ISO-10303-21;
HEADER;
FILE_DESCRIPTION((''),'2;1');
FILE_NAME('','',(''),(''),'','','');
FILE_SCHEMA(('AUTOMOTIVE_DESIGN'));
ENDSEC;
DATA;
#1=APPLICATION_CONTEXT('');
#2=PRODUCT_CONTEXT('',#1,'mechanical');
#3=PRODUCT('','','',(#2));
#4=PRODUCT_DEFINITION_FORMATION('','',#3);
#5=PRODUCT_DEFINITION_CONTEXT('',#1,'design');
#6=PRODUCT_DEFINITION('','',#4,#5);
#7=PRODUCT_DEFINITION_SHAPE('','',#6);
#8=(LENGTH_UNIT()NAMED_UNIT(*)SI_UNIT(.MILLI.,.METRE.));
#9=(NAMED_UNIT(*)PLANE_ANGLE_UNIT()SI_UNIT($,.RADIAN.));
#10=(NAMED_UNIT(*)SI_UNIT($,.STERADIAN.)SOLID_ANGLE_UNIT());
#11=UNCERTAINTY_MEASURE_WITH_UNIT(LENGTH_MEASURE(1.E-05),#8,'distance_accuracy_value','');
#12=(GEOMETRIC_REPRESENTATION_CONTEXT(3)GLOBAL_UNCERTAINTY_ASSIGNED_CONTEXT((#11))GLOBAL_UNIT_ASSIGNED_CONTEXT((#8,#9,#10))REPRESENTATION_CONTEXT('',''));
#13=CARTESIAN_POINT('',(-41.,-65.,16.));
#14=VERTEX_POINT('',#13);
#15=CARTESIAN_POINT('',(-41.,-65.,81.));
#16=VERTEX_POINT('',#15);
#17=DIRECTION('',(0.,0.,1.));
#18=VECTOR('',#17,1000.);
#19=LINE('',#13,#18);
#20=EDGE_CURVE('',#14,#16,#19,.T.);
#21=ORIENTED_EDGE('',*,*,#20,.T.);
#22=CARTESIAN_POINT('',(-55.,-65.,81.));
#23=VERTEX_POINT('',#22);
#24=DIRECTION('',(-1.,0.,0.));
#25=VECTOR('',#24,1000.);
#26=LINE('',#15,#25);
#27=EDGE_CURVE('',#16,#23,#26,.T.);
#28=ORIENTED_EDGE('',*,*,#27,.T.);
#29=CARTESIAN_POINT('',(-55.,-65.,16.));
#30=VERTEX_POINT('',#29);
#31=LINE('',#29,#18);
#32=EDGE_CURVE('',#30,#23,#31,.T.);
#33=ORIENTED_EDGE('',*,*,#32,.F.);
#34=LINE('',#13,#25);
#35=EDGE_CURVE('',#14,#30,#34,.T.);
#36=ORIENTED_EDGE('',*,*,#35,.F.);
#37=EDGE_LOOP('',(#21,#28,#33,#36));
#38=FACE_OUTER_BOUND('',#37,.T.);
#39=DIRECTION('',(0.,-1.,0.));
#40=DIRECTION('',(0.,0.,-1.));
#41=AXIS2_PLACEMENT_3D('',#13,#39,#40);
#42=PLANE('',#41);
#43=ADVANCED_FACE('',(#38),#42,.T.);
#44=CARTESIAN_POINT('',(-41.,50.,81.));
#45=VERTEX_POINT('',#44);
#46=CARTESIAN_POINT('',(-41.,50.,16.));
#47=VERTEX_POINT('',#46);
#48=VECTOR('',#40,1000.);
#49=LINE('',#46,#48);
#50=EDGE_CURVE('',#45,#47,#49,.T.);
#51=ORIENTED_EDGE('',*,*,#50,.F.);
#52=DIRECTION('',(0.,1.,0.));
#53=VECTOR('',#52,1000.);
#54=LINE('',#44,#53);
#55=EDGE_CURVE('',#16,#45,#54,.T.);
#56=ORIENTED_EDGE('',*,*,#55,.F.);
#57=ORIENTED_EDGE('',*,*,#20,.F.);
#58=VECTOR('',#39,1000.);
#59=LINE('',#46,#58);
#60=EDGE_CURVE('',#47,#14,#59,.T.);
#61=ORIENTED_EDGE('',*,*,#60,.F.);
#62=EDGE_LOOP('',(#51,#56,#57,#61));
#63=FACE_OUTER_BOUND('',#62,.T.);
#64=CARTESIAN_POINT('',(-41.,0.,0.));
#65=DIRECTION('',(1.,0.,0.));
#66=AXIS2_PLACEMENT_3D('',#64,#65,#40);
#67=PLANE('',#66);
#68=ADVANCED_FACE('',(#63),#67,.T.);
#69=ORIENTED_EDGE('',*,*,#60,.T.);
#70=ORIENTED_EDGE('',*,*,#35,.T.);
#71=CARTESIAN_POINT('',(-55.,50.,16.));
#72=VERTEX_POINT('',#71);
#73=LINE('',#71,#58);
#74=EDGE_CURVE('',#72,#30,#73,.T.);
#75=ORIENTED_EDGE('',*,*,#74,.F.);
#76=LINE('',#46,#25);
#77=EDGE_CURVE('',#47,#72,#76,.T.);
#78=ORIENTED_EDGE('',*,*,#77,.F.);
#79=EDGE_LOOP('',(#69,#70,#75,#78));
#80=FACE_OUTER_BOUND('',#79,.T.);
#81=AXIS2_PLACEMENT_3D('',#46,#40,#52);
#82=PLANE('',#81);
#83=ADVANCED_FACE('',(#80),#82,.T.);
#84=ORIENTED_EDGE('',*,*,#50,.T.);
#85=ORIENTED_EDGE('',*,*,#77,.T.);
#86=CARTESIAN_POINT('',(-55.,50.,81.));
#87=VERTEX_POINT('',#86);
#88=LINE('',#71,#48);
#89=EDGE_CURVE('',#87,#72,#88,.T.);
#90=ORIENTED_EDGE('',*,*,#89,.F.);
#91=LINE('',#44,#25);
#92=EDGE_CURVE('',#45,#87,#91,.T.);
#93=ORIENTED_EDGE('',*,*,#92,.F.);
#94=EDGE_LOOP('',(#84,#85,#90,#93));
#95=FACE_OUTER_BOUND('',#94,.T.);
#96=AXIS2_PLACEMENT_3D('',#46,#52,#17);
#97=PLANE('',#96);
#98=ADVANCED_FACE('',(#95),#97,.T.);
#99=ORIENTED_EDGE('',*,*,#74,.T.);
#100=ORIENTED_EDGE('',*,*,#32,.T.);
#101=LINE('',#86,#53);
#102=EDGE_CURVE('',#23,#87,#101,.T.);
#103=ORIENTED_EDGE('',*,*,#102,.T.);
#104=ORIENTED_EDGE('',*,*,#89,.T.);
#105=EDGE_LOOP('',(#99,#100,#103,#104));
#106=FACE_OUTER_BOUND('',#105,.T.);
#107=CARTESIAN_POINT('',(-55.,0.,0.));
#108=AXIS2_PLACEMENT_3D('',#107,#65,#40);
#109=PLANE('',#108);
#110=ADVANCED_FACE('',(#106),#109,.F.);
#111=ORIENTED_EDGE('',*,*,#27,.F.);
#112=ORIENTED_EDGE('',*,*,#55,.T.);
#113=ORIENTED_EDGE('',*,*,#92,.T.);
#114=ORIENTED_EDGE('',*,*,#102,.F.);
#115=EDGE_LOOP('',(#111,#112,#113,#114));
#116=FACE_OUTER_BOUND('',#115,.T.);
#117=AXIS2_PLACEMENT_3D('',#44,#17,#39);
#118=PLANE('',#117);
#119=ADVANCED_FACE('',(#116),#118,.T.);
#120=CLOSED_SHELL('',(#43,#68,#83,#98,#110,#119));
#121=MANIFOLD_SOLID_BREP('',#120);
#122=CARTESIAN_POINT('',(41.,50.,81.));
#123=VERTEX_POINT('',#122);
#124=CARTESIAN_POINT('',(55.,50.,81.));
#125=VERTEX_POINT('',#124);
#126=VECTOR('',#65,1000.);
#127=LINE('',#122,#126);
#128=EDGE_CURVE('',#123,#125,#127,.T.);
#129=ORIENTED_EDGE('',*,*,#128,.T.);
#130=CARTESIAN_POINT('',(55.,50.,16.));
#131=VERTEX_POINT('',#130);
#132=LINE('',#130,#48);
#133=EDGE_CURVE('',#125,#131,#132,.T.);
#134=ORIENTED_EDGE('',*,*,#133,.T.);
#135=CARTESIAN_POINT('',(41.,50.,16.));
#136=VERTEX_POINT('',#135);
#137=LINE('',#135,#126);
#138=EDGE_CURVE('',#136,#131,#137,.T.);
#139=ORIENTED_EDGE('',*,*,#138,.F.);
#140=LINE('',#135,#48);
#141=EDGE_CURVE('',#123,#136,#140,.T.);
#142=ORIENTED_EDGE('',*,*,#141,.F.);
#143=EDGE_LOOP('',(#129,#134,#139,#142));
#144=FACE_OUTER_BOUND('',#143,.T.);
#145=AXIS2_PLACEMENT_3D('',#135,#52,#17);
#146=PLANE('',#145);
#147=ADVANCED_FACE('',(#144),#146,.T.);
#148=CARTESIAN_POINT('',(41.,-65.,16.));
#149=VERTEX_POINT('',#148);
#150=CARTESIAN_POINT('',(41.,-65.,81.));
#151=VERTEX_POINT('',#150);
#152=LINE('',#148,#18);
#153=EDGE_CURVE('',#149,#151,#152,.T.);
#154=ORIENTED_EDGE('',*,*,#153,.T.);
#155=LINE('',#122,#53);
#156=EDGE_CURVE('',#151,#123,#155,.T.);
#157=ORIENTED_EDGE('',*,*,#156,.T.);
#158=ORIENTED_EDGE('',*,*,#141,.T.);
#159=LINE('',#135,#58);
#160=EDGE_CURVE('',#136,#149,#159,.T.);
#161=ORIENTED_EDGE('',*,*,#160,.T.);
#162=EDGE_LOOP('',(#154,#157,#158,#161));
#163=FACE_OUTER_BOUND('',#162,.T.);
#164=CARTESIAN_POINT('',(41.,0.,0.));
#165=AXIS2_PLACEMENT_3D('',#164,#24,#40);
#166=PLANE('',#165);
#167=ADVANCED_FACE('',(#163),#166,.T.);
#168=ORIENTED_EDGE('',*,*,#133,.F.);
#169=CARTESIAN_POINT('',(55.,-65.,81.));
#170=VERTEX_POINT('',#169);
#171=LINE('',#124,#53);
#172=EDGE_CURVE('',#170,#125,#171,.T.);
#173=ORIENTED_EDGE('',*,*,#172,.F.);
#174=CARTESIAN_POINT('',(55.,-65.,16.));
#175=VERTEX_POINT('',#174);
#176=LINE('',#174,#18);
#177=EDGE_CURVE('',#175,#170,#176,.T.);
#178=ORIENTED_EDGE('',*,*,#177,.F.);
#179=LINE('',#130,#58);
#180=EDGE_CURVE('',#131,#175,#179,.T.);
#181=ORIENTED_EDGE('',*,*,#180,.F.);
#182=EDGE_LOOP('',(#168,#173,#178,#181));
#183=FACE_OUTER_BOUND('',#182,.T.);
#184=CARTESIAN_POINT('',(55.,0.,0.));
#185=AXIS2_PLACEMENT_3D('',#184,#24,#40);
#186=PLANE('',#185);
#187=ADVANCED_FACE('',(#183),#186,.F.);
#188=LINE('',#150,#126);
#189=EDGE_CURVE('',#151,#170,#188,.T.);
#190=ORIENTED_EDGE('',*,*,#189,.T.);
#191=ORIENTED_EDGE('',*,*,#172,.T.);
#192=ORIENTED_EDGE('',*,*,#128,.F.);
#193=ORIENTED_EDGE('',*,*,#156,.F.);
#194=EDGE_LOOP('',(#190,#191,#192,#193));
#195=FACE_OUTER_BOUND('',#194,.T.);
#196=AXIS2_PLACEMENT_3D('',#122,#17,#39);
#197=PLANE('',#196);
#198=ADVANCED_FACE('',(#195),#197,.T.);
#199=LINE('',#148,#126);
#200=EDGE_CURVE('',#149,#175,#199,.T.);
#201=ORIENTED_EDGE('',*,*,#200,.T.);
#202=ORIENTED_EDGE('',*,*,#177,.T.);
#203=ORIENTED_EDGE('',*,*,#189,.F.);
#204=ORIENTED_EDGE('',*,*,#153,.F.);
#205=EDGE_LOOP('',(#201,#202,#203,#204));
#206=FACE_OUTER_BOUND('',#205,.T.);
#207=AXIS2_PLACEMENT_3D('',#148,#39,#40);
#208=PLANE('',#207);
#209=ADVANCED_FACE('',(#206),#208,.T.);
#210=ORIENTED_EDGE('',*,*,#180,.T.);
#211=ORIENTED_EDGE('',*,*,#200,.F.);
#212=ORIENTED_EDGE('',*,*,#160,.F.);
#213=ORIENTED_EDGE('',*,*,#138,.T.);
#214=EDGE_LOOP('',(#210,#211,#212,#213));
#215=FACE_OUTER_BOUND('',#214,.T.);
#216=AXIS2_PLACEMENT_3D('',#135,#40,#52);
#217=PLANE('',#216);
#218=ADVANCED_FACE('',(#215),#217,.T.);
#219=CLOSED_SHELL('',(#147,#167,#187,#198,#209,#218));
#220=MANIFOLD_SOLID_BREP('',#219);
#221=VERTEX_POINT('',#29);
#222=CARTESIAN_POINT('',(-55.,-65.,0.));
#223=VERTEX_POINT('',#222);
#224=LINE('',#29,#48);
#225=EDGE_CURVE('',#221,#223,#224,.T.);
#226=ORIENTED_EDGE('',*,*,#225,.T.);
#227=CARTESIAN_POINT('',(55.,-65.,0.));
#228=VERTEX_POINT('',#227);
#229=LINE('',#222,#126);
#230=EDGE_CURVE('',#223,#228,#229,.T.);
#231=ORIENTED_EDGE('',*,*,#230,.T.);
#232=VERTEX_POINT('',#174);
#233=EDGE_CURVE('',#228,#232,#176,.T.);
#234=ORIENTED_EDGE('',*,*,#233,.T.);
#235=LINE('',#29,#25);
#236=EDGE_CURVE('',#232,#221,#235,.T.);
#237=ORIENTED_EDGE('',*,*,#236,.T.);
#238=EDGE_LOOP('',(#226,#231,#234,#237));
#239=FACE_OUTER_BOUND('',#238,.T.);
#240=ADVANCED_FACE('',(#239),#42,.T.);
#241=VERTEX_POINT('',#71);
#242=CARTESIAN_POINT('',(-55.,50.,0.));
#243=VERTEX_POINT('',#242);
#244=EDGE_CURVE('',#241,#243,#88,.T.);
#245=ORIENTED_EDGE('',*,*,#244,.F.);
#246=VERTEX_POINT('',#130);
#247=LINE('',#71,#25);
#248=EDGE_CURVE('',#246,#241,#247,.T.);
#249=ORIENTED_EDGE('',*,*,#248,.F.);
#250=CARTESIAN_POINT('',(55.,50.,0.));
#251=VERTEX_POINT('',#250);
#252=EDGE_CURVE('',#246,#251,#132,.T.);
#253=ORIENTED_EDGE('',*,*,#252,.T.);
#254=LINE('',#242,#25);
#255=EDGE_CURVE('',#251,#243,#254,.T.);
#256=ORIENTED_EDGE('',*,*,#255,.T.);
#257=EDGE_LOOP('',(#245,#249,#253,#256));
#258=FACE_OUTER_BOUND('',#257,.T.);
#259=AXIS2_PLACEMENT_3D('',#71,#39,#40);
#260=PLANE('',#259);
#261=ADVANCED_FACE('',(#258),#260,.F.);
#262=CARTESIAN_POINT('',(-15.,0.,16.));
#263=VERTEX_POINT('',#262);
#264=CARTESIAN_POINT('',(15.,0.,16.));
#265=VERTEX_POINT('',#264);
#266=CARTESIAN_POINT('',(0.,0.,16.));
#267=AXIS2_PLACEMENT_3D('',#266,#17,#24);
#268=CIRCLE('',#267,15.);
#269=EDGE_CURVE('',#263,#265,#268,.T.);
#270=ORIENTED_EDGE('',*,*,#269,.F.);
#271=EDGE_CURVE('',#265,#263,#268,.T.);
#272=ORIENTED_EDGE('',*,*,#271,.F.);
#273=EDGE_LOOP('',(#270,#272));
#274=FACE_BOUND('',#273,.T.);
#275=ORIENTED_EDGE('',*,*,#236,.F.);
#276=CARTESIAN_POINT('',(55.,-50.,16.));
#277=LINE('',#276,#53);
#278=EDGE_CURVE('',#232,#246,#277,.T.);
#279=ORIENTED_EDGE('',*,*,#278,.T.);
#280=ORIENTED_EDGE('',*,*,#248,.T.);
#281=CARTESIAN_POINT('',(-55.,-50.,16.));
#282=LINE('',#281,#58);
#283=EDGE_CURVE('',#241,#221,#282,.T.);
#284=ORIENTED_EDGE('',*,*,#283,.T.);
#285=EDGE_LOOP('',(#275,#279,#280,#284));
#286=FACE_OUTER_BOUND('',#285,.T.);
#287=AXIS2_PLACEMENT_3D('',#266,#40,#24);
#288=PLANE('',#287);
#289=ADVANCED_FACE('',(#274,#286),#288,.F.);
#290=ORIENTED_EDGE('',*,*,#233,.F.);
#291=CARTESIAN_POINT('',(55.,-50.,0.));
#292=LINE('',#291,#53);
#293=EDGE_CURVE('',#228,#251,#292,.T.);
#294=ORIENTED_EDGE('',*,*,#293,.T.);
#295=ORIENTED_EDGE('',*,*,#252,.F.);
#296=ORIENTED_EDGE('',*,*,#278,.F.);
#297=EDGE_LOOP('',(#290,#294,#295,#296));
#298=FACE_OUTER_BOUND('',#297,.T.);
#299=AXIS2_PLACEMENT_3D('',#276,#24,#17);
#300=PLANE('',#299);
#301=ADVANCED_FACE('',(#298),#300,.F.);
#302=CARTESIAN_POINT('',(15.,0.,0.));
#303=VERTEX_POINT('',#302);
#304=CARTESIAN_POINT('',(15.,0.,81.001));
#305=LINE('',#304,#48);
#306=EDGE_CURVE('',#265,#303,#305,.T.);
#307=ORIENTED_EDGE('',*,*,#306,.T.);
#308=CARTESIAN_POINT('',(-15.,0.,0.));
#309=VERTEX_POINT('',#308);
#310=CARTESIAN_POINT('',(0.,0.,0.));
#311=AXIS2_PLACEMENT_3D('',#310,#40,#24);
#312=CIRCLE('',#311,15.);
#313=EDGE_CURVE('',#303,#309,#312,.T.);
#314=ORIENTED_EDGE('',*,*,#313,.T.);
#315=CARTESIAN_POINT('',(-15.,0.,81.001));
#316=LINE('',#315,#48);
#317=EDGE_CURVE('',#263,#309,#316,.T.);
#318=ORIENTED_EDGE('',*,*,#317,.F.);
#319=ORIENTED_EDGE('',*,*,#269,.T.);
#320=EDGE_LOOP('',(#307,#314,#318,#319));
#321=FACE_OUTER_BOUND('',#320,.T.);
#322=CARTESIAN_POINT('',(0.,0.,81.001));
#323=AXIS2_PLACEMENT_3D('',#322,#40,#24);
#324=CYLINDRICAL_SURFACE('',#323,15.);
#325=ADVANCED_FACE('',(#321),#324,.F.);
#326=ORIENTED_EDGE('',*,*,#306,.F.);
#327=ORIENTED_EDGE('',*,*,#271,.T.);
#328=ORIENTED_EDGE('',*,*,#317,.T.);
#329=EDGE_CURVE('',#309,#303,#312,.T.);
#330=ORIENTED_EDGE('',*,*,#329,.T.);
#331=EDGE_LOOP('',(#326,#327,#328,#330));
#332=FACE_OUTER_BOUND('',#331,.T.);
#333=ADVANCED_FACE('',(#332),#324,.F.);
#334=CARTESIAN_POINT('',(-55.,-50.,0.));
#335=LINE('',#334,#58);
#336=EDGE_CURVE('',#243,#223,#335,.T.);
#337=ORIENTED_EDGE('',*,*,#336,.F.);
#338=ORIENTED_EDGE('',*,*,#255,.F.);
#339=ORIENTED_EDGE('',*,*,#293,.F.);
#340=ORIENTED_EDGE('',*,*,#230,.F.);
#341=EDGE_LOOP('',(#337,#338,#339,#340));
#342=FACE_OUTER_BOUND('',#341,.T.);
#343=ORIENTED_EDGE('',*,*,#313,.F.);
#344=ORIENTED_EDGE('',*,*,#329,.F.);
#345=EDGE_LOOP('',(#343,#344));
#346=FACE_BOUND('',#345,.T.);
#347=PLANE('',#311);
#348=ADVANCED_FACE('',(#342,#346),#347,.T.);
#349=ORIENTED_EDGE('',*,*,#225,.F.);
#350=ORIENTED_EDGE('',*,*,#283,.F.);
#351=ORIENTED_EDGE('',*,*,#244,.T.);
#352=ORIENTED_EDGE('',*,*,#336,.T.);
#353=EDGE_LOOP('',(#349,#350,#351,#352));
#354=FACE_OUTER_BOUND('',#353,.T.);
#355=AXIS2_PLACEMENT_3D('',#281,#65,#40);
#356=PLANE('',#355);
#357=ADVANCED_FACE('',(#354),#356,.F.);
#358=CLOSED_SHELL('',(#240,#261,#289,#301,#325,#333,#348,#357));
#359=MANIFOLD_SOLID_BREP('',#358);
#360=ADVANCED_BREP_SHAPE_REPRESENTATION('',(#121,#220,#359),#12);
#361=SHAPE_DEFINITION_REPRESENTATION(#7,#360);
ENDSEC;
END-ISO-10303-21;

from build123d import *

# Parameters (mm, degrees)
SKETCH_1_W          = 110
SKETCH_1_H          = 100
EXTRUDE_1_DEPTH     = 16
SKETCH_2_W          = 65
SKETCH_2_H          = 115
EXTRUDE_2_DEPTH     = 14
SKETCH_3_R          = 15
CUT_EXTRUDE_1_DEPTH = 16
SKETCH_4_W          = 110
SKETCH_4_H          = 16
EXTRUDE_3_DEPTH     = 15


with BuildPart() as part:
    # 草图1 → 凸台-拉伸1 (new body)
    with BuildSketch(Plane.XY):
        Rectangle(SKETCH_1_W, SKETCH_1_H)
    extrude(amount=EXTRUDE_1_DEPTH)

    # 草图3 → 切除-拉伸1 (cut)
    with BuildSketch(Plane(origin=(0, 0, 0), x_dir=(-1, 0, 0), z_dir=(0, 0, -1))):
        Circle(SKETCH_3_R)
    extrude(amount=-CUT_EXTRUDE_1_DEPTH, mode=Mode.SUBTRACT)

    # 草图4 → 凸台-拉伸3 (add)
    with BuildSketch(Plane.XZ.offset(50)):
        with Locations((0, 8)):
            Rectangle(SKETCH_4_W, SKETCH_4_H)
    extrude(amount=EXTRUDE_3_DEPTH)


with BuildPart() as body_2:
    # 草图2 → 凸台-拉伸2 (new body)
    with BuildSketch(Plane.ZY.offset(55)):
        with Locations((48.5, -7.5)):
            Rectangle(SKETCH_2_W, SKETCH_2_H)
    extrude(amount=-EXTRUDE_2_DEPTH)


with BuildPart() as body_3:
    # 镜向1: mirrored copy
    add(body_2.part.mirror(Plane(origin=(0, 0, 0), x_dir=(0, 0, 1), z_dir=(1, 0, 0))))


solid = Compound([part.part, body_2.part, body_3.part])
